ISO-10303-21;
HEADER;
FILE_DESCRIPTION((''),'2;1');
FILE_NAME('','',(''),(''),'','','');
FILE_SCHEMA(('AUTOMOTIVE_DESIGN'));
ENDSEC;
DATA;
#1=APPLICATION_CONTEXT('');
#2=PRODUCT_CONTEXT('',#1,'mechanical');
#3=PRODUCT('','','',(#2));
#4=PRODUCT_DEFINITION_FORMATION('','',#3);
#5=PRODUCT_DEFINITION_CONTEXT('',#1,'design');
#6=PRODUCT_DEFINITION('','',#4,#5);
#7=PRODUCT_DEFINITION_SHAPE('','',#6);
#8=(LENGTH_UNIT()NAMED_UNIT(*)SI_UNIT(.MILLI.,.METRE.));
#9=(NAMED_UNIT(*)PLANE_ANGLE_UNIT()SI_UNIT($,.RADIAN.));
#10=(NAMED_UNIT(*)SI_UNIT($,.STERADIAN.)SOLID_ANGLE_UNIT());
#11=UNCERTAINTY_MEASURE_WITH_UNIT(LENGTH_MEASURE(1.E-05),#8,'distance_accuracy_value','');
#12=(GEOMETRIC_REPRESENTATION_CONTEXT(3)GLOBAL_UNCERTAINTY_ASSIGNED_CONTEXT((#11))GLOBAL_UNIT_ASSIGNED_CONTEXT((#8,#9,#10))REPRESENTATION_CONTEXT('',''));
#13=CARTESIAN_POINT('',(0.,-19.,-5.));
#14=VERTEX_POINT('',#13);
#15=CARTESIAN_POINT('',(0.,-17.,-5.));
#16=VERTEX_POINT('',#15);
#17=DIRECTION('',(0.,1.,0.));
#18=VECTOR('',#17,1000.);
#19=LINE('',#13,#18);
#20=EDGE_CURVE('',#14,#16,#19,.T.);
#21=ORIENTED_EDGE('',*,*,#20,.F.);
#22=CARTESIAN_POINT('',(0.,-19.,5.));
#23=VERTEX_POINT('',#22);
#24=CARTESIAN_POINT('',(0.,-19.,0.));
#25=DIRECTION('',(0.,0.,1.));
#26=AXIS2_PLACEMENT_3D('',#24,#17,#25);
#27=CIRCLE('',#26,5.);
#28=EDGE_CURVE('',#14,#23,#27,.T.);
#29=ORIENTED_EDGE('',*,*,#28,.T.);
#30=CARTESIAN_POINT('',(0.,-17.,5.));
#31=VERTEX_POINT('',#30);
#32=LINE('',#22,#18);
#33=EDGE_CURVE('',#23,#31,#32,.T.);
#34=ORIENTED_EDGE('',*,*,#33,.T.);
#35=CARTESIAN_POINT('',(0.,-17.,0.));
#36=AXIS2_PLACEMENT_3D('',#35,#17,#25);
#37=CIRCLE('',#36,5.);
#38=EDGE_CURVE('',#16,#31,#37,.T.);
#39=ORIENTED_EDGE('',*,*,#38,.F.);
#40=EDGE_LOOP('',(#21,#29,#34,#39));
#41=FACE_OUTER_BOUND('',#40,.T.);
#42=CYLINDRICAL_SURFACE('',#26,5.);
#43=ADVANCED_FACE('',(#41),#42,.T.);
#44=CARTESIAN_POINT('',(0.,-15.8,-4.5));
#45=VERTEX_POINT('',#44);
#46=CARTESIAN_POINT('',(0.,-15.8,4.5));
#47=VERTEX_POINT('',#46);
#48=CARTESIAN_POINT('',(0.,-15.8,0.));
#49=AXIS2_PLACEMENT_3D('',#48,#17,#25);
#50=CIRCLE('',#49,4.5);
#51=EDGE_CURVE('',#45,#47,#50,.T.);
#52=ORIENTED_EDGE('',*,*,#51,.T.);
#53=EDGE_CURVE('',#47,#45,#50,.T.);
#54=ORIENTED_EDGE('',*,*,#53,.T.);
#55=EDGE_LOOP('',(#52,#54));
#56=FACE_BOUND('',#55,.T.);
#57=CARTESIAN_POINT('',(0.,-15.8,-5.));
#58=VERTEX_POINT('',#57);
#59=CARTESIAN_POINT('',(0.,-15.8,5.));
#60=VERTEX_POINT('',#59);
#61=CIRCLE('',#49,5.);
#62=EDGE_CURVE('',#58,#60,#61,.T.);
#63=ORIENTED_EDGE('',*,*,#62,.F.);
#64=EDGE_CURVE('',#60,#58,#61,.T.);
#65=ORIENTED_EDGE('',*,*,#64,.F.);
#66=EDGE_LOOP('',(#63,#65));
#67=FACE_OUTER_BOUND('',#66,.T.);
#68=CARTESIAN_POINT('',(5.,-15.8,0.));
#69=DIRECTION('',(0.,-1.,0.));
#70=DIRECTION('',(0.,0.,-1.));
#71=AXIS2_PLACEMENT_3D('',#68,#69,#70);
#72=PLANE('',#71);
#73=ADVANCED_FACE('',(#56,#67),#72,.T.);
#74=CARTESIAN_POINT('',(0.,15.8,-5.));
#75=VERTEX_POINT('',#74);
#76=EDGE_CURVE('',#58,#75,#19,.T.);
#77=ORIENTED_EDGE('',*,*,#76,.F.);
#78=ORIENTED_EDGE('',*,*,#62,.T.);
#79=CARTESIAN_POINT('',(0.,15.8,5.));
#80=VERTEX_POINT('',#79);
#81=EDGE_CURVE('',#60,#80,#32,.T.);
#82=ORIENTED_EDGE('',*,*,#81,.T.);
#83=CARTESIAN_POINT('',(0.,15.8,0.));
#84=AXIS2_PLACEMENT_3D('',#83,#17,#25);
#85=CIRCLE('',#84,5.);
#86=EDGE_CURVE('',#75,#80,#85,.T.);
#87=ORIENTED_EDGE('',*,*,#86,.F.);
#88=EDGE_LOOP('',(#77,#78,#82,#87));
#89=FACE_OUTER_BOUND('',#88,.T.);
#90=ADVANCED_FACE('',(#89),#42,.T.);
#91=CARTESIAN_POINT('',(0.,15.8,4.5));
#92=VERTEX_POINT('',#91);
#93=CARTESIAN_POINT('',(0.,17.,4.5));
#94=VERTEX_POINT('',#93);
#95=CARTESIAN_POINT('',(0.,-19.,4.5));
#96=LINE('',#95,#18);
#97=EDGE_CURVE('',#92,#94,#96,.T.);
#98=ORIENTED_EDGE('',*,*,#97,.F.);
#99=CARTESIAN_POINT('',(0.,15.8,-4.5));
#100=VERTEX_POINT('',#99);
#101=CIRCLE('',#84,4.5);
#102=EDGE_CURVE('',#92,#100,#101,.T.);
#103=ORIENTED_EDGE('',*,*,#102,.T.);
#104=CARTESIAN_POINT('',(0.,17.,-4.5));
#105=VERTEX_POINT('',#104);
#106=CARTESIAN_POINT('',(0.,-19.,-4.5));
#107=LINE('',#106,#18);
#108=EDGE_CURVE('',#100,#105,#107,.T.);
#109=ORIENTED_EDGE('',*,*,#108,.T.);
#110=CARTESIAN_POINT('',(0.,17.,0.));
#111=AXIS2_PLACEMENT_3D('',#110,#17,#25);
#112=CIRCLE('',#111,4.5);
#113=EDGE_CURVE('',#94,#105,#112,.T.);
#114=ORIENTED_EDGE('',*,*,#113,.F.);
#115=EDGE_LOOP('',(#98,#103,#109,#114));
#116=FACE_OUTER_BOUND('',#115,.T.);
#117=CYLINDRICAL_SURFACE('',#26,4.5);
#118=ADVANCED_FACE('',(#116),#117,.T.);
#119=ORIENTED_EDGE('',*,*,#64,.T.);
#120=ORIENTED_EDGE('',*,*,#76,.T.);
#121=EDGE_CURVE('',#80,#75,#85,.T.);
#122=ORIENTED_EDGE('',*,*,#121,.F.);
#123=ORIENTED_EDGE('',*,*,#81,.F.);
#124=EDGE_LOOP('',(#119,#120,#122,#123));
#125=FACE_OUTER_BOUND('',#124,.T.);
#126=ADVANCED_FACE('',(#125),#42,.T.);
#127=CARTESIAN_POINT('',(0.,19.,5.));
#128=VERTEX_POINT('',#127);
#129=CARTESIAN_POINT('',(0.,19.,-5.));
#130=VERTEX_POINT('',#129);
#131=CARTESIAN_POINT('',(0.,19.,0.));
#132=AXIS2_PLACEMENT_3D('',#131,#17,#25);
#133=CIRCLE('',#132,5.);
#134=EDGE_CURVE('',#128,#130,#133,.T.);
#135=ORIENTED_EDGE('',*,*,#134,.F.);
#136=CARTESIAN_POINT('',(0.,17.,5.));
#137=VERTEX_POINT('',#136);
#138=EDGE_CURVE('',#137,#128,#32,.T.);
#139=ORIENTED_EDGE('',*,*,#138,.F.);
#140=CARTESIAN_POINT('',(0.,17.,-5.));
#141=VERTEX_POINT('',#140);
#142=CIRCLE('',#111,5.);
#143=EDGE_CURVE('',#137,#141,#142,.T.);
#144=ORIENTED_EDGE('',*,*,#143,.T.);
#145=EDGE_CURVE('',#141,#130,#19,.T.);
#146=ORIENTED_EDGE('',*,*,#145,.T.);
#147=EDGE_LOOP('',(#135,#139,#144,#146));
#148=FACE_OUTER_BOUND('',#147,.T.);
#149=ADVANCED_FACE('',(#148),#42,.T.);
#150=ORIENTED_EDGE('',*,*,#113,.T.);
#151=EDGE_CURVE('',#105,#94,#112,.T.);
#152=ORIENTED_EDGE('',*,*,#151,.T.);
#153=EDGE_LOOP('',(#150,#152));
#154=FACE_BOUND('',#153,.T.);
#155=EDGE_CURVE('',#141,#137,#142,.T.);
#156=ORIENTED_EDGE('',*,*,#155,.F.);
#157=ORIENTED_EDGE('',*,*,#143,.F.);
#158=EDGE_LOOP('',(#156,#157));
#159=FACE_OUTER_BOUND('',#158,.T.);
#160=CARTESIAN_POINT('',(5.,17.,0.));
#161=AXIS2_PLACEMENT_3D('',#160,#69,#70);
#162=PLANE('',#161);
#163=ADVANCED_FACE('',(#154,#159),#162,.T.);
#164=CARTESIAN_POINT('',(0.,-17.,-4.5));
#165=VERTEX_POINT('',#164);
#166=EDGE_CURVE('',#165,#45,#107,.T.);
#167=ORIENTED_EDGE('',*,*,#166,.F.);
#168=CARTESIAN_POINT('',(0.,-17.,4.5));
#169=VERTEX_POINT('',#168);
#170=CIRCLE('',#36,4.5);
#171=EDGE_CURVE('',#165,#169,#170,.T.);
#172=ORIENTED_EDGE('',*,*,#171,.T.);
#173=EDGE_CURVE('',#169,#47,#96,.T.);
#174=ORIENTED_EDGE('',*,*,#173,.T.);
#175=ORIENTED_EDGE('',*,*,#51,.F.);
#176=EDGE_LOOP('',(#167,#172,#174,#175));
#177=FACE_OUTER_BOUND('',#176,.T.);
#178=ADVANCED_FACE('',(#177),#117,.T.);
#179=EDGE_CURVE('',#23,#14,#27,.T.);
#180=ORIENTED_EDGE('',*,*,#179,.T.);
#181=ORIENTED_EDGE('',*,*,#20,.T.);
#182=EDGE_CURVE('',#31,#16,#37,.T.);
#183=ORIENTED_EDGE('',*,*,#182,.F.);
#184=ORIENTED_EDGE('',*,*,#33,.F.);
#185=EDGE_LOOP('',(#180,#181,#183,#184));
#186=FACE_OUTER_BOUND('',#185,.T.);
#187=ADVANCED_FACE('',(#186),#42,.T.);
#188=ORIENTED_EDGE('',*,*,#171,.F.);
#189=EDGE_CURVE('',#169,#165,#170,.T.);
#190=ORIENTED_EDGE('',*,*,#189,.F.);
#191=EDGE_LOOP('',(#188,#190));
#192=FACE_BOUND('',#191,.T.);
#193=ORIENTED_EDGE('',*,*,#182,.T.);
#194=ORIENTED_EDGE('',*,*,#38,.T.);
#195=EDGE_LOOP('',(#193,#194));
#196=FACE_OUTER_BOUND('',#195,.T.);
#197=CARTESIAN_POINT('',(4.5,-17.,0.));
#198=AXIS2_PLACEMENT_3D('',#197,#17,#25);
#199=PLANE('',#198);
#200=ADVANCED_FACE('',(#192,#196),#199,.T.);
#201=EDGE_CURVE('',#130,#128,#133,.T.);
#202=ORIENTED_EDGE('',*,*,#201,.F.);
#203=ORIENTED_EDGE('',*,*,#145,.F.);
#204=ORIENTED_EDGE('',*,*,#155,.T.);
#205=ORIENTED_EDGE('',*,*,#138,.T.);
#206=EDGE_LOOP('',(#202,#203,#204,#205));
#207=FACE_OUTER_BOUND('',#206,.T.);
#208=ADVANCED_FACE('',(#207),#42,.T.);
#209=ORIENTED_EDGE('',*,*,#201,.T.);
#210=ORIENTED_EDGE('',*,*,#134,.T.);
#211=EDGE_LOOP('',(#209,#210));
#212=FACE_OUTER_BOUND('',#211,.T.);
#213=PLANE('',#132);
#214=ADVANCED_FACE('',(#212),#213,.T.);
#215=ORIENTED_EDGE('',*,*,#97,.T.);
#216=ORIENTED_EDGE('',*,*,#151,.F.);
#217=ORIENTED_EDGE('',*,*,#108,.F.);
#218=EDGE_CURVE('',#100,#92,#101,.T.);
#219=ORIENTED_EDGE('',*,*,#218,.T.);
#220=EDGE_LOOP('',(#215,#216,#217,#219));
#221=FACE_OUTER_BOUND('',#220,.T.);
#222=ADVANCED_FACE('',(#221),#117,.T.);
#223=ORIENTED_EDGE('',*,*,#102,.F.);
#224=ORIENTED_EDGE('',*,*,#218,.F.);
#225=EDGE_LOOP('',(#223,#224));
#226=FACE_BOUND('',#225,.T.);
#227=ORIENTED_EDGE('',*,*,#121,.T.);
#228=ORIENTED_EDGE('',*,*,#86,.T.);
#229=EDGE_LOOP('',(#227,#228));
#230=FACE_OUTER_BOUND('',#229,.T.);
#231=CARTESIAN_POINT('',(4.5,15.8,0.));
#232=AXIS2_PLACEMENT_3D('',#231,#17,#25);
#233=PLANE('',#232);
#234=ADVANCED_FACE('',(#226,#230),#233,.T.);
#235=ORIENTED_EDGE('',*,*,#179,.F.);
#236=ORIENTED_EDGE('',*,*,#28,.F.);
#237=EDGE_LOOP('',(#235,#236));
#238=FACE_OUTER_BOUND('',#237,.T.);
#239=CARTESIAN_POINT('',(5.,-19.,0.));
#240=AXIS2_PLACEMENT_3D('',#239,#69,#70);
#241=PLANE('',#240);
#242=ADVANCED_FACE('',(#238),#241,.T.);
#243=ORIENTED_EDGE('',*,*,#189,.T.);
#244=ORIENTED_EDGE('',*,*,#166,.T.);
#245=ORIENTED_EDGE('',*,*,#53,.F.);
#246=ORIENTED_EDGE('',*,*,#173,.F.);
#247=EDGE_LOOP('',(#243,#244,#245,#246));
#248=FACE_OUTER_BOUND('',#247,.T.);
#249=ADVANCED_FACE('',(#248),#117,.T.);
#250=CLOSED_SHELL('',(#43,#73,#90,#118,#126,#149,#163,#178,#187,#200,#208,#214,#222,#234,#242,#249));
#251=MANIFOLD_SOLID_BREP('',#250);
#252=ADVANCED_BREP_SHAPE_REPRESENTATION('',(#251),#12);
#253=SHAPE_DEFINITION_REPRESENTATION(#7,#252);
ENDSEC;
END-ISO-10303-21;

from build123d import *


with BuildPart() as part:
    # 草图1 → 旋转1 (revolve)
    with BuildSketch(Plane(origin=(0, 0, 0), x_dir=(-1, 0, 0), z_dir=(0, 0, -1)), mode=Mode.PRIVATE) as revolve_1_sk:
        Polygon((-5, -19), (0, -19), (0, 19), (-5, 19), (-5, 17), (-4.5, 17), (-4.5, 15.8), (-5, 15.8), (-5, -15.8), (-4.5, -15.8), (-4.5, -17), (-5, -17), align=None)
    revolve(revolve_1_sk.sketch.rotate(Axis((0, -19, 0), (0, 1, 0)), 270), axis=Axis((0, -19, 0), (0, 1, 0)))


solid = part.part
